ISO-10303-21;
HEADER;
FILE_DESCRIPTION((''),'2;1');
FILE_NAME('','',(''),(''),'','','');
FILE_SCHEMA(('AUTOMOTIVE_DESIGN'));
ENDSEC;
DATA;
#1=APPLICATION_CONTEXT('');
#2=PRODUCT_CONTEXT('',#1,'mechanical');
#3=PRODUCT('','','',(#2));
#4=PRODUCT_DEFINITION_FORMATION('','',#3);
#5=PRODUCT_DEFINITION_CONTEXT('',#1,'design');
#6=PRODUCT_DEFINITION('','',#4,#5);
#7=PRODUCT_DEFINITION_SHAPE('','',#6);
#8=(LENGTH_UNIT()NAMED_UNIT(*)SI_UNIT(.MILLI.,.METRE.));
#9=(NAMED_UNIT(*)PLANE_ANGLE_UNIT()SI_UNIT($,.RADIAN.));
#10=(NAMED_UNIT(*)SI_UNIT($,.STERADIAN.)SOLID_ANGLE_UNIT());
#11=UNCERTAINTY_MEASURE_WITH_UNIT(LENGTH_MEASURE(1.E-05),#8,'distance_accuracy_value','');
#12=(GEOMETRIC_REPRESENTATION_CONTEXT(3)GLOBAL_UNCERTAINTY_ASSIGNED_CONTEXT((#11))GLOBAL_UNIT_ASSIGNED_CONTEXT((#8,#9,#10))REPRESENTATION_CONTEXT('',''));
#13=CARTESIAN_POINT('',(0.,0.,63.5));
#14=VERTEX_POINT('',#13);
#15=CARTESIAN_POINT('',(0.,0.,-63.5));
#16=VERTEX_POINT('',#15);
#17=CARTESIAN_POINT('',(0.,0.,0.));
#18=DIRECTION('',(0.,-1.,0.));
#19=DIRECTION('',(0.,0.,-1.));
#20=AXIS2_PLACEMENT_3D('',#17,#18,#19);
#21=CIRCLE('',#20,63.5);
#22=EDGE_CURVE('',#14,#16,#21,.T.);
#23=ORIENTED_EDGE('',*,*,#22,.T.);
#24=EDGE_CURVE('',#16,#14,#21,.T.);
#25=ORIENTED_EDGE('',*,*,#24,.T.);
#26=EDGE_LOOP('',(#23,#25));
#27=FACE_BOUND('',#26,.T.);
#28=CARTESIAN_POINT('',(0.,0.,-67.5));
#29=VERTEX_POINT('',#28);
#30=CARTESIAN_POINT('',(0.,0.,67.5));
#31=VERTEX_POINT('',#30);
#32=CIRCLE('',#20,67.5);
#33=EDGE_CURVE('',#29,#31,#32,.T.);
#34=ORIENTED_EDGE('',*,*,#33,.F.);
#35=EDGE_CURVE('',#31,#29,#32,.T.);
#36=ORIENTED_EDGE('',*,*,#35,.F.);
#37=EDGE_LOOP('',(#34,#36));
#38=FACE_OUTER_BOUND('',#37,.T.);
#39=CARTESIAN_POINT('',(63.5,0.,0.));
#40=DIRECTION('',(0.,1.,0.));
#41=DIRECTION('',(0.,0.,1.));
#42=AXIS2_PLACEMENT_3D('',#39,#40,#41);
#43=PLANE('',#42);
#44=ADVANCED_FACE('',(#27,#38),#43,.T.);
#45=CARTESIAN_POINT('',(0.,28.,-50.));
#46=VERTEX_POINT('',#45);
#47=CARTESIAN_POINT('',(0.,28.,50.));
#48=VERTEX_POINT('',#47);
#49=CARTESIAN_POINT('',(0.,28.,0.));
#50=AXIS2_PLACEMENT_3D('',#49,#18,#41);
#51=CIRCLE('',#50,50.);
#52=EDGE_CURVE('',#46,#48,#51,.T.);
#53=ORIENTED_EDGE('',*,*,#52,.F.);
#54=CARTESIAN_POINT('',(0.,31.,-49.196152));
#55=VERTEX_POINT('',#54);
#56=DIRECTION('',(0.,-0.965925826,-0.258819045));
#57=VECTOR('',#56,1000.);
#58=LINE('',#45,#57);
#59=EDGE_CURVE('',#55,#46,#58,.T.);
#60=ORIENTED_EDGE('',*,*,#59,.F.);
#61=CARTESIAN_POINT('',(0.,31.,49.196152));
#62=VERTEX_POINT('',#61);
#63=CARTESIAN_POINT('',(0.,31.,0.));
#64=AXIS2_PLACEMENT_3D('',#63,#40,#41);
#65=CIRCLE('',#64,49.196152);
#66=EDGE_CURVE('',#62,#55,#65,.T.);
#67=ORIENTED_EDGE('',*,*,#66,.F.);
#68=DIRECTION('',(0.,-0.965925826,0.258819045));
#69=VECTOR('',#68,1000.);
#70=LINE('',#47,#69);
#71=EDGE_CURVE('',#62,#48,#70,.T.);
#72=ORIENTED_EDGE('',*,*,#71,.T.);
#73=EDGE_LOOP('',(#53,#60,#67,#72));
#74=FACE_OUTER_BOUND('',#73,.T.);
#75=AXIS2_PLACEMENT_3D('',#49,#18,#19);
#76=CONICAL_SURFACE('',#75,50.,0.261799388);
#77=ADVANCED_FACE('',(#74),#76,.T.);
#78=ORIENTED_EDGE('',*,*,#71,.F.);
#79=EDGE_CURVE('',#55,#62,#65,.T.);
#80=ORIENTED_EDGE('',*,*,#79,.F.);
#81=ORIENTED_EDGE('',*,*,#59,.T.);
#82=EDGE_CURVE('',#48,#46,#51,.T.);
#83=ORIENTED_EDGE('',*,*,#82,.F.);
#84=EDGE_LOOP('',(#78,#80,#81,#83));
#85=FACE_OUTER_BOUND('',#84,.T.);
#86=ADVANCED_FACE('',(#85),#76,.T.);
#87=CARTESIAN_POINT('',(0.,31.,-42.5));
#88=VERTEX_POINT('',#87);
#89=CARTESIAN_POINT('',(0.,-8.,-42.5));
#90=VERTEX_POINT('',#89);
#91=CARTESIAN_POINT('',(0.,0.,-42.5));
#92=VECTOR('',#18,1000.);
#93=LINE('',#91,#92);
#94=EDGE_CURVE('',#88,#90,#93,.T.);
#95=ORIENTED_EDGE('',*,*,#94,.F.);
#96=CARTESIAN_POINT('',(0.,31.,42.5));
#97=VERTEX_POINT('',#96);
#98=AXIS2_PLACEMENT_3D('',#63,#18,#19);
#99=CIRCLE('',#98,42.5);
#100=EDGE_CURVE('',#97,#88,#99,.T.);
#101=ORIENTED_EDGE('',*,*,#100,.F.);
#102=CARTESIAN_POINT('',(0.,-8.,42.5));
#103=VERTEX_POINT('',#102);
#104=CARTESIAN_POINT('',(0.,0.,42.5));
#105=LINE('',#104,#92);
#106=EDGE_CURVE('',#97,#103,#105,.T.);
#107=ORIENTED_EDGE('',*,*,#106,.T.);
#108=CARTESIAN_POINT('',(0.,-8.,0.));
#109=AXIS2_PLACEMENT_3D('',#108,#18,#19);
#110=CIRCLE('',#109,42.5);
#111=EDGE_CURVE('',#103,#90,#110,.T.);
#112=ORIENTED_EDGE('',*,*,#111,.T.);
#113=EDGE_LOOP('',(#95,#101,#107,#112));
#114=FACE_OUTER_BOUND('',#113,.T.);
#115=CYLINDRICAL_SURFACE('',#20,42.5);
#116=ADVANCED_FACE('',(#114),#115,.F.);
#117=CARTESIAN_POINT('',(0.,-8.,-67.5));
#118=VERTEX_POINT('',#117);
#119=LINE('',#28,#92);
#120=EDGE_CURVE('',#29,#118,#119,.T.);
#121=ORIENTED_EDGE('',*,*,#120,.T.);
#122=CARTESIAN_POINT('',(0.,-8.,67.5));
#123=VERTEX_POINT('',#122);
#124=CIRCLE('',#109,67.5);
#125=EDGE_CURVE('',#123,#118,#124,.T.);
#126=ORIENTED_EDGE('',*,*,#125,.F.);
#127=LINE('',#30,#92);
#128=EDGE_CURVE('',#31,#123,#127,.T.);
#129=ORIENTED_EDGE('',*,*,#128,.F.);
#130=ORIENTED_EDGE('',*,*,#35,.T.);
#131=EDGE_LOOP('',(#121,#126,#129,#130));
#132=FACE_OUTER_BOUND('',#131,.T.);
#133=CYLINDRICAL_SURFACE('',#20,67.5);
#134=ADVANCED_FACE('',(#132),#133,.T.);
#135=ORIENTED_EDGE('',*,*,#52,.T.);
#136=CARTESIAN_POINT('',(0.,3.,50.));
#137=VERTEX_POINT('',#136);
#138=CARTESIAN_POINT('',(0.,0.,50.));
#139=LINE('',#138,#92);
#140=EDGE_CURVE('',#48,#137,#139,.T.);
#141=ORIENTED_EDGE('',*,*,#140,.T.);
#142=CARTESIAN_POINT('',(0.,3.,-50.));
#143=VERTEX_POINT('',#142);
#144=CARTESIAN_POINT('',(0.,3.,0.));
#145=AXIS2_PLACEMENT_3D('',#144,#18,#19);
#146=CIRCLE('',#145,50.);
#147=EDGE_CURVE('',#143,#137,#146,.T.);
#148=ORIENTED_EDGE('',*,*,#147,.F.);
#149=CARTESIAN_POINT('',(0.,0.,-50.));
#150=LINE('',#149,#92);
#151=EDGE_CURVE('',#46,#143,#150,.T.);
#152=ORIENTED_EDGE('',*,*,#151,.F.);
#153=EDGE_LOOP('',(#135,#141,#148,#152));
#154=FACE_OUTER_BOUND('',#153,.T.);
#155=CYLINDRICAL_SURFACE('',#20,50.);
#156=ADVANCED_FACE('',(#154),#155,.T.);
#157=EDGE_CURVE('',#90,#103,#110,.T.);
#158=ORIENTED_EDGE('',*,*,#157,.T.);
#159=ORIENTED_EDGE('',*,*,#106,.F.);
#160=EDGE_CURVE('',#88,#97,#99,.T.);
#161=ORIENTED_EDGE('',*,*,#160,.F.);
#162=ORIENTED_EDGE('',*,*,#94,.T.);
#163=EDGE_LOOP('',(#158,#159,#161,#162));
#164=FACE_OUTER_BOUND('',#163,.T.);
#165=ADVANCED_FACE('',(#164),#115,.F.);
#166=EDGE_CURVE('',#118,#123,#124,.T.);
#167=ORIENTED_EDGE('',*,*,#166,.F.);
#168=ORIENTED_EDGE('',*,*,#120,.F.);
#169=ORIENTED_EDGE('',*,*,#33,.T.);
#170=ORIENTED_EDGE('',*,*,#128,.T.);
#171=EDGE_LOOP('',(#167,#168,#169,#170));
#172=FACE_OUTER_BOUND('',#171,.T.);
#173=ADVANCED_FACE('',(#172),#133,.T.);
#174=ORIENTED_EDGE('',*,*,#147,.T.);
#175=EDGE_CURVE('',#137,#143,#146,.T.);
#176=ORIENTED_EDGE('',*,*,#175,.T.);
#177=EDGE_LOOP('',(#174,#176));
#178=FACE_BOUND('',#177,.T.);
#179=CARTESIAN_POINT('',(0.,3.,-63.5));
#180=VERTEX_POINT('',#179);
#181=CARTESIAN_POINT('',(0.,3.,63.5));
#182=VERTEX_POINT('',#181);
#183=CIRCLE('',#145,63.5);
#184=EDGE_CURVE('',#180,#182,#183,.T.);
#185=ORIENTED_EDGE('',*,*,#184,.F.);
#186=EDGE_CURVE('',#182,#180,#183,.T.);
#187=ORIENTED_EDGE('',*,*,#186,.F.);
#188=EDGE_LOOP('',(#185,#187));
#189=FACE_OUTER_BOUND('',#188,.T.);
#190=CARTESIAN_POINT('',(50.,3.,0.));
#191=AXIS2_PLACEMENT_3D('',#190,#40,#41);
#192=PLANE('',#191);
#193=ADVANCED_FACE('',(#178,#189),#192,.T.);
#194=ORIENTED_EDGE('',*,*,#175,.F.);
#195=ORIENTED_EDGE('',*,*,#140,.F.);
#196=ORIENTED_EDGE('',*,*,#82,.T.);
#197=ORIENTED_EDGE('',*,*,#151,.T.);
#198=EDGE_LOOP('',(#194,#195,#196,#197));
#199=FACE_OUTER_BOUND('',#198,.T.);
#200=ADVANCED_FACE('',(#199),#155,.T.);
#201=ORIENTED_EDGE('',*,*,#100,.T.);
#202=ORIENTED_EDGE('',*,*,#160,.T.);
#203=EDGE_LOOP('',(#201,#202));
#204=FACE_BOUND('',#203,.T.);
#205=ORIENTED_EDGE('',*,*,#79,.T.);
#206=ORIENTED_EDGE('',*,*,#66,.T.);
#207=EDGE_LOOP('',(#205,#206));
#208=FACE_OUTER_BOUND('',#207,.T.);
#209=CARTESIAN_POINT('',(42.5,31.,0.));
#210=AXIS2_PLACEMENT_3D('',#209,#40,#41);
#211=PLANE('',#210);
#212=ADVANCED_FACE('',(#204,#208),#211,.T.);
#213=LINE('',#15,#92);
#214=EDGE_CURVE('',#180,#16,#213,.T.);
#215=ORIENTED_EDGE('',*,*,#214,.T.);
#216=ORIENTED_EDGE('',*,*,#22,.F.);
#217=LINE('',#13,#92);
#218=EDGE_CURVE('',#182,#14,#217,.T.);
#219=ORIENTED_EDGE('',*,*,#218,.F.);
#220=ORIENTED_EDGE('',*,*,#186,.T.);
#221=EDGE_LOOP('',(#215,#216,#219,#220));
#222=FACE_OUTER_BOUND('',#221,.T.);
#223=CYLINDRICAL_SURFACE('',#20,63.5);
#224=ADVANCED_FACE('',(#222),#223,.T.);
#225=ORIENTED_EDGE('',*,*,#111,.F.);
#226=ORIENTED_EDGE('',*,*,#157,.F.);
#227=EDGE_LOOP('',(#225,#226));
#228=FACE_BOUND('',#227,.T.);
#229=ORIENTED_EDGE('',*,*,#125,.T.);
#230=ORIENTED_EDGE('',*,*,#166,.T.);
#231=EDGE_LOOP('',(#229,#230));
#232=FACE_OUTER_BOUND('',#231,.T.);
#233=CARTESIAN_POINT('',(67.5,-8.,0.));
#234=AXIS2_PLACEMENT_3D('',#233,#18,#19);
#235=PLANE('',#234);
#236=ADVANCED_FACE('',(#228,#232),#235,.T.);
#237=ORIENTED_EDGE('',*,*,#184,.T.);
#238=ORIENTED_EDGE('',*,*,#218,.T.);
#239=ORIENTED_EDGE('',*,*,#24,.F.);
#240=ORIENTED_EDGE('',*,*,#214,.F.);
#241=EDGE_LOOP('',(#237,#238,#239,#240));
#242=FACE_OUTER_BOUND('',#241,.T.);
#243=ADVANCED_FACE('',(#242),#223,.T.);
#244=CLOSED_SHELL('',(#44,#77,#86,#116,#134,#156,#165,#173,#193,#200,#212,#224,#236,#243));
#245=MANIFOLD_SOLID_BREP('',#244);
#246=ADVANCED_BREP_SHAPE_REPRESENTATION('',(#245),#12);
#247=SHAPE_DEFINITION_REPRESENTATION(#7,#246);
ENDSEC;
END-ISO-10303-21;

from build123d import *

# Parameters (mm, degrees)
CHAMFER1_SIZE  = 3
CHAMFER1_SIZE2 = 0.803847577


with BuildPart() as part:
    # Sketch1 → Revolve1 (revolve)
    with BuildSketch(Plane.XY, mode=Mode.PRIVATE) as revolve1_sk:
        Polygon((42.5, 31), (50, 31), (50, 3), (63.5, 3), (63.5, 0), (67.5, 0), (67.5, -8), (42.5, -8), align=None)
    revolve(revolve1_sk.sketch.rotate(Axis((0, 0, 0), (0, 1, 0)), 90), axis=Axis((0, 0, 0), (0, 1, 0)))

    # Chamfer1
    chamfer1_edges = [part.edges().sort_by_distance(p)[0] for p in [
        (0, 31, 50),
    ]]
    chamfer1_side = [part.faces().sort_by_distance(p)[0] for p in [
        (0, 17, 50),
    ]]
    chamfer(chamfer1_edges, length=CHAMFER1_SIZE, length2=CHAMFER1_SIZE2, reference=chamfer1_side[0])


solid = part.part
